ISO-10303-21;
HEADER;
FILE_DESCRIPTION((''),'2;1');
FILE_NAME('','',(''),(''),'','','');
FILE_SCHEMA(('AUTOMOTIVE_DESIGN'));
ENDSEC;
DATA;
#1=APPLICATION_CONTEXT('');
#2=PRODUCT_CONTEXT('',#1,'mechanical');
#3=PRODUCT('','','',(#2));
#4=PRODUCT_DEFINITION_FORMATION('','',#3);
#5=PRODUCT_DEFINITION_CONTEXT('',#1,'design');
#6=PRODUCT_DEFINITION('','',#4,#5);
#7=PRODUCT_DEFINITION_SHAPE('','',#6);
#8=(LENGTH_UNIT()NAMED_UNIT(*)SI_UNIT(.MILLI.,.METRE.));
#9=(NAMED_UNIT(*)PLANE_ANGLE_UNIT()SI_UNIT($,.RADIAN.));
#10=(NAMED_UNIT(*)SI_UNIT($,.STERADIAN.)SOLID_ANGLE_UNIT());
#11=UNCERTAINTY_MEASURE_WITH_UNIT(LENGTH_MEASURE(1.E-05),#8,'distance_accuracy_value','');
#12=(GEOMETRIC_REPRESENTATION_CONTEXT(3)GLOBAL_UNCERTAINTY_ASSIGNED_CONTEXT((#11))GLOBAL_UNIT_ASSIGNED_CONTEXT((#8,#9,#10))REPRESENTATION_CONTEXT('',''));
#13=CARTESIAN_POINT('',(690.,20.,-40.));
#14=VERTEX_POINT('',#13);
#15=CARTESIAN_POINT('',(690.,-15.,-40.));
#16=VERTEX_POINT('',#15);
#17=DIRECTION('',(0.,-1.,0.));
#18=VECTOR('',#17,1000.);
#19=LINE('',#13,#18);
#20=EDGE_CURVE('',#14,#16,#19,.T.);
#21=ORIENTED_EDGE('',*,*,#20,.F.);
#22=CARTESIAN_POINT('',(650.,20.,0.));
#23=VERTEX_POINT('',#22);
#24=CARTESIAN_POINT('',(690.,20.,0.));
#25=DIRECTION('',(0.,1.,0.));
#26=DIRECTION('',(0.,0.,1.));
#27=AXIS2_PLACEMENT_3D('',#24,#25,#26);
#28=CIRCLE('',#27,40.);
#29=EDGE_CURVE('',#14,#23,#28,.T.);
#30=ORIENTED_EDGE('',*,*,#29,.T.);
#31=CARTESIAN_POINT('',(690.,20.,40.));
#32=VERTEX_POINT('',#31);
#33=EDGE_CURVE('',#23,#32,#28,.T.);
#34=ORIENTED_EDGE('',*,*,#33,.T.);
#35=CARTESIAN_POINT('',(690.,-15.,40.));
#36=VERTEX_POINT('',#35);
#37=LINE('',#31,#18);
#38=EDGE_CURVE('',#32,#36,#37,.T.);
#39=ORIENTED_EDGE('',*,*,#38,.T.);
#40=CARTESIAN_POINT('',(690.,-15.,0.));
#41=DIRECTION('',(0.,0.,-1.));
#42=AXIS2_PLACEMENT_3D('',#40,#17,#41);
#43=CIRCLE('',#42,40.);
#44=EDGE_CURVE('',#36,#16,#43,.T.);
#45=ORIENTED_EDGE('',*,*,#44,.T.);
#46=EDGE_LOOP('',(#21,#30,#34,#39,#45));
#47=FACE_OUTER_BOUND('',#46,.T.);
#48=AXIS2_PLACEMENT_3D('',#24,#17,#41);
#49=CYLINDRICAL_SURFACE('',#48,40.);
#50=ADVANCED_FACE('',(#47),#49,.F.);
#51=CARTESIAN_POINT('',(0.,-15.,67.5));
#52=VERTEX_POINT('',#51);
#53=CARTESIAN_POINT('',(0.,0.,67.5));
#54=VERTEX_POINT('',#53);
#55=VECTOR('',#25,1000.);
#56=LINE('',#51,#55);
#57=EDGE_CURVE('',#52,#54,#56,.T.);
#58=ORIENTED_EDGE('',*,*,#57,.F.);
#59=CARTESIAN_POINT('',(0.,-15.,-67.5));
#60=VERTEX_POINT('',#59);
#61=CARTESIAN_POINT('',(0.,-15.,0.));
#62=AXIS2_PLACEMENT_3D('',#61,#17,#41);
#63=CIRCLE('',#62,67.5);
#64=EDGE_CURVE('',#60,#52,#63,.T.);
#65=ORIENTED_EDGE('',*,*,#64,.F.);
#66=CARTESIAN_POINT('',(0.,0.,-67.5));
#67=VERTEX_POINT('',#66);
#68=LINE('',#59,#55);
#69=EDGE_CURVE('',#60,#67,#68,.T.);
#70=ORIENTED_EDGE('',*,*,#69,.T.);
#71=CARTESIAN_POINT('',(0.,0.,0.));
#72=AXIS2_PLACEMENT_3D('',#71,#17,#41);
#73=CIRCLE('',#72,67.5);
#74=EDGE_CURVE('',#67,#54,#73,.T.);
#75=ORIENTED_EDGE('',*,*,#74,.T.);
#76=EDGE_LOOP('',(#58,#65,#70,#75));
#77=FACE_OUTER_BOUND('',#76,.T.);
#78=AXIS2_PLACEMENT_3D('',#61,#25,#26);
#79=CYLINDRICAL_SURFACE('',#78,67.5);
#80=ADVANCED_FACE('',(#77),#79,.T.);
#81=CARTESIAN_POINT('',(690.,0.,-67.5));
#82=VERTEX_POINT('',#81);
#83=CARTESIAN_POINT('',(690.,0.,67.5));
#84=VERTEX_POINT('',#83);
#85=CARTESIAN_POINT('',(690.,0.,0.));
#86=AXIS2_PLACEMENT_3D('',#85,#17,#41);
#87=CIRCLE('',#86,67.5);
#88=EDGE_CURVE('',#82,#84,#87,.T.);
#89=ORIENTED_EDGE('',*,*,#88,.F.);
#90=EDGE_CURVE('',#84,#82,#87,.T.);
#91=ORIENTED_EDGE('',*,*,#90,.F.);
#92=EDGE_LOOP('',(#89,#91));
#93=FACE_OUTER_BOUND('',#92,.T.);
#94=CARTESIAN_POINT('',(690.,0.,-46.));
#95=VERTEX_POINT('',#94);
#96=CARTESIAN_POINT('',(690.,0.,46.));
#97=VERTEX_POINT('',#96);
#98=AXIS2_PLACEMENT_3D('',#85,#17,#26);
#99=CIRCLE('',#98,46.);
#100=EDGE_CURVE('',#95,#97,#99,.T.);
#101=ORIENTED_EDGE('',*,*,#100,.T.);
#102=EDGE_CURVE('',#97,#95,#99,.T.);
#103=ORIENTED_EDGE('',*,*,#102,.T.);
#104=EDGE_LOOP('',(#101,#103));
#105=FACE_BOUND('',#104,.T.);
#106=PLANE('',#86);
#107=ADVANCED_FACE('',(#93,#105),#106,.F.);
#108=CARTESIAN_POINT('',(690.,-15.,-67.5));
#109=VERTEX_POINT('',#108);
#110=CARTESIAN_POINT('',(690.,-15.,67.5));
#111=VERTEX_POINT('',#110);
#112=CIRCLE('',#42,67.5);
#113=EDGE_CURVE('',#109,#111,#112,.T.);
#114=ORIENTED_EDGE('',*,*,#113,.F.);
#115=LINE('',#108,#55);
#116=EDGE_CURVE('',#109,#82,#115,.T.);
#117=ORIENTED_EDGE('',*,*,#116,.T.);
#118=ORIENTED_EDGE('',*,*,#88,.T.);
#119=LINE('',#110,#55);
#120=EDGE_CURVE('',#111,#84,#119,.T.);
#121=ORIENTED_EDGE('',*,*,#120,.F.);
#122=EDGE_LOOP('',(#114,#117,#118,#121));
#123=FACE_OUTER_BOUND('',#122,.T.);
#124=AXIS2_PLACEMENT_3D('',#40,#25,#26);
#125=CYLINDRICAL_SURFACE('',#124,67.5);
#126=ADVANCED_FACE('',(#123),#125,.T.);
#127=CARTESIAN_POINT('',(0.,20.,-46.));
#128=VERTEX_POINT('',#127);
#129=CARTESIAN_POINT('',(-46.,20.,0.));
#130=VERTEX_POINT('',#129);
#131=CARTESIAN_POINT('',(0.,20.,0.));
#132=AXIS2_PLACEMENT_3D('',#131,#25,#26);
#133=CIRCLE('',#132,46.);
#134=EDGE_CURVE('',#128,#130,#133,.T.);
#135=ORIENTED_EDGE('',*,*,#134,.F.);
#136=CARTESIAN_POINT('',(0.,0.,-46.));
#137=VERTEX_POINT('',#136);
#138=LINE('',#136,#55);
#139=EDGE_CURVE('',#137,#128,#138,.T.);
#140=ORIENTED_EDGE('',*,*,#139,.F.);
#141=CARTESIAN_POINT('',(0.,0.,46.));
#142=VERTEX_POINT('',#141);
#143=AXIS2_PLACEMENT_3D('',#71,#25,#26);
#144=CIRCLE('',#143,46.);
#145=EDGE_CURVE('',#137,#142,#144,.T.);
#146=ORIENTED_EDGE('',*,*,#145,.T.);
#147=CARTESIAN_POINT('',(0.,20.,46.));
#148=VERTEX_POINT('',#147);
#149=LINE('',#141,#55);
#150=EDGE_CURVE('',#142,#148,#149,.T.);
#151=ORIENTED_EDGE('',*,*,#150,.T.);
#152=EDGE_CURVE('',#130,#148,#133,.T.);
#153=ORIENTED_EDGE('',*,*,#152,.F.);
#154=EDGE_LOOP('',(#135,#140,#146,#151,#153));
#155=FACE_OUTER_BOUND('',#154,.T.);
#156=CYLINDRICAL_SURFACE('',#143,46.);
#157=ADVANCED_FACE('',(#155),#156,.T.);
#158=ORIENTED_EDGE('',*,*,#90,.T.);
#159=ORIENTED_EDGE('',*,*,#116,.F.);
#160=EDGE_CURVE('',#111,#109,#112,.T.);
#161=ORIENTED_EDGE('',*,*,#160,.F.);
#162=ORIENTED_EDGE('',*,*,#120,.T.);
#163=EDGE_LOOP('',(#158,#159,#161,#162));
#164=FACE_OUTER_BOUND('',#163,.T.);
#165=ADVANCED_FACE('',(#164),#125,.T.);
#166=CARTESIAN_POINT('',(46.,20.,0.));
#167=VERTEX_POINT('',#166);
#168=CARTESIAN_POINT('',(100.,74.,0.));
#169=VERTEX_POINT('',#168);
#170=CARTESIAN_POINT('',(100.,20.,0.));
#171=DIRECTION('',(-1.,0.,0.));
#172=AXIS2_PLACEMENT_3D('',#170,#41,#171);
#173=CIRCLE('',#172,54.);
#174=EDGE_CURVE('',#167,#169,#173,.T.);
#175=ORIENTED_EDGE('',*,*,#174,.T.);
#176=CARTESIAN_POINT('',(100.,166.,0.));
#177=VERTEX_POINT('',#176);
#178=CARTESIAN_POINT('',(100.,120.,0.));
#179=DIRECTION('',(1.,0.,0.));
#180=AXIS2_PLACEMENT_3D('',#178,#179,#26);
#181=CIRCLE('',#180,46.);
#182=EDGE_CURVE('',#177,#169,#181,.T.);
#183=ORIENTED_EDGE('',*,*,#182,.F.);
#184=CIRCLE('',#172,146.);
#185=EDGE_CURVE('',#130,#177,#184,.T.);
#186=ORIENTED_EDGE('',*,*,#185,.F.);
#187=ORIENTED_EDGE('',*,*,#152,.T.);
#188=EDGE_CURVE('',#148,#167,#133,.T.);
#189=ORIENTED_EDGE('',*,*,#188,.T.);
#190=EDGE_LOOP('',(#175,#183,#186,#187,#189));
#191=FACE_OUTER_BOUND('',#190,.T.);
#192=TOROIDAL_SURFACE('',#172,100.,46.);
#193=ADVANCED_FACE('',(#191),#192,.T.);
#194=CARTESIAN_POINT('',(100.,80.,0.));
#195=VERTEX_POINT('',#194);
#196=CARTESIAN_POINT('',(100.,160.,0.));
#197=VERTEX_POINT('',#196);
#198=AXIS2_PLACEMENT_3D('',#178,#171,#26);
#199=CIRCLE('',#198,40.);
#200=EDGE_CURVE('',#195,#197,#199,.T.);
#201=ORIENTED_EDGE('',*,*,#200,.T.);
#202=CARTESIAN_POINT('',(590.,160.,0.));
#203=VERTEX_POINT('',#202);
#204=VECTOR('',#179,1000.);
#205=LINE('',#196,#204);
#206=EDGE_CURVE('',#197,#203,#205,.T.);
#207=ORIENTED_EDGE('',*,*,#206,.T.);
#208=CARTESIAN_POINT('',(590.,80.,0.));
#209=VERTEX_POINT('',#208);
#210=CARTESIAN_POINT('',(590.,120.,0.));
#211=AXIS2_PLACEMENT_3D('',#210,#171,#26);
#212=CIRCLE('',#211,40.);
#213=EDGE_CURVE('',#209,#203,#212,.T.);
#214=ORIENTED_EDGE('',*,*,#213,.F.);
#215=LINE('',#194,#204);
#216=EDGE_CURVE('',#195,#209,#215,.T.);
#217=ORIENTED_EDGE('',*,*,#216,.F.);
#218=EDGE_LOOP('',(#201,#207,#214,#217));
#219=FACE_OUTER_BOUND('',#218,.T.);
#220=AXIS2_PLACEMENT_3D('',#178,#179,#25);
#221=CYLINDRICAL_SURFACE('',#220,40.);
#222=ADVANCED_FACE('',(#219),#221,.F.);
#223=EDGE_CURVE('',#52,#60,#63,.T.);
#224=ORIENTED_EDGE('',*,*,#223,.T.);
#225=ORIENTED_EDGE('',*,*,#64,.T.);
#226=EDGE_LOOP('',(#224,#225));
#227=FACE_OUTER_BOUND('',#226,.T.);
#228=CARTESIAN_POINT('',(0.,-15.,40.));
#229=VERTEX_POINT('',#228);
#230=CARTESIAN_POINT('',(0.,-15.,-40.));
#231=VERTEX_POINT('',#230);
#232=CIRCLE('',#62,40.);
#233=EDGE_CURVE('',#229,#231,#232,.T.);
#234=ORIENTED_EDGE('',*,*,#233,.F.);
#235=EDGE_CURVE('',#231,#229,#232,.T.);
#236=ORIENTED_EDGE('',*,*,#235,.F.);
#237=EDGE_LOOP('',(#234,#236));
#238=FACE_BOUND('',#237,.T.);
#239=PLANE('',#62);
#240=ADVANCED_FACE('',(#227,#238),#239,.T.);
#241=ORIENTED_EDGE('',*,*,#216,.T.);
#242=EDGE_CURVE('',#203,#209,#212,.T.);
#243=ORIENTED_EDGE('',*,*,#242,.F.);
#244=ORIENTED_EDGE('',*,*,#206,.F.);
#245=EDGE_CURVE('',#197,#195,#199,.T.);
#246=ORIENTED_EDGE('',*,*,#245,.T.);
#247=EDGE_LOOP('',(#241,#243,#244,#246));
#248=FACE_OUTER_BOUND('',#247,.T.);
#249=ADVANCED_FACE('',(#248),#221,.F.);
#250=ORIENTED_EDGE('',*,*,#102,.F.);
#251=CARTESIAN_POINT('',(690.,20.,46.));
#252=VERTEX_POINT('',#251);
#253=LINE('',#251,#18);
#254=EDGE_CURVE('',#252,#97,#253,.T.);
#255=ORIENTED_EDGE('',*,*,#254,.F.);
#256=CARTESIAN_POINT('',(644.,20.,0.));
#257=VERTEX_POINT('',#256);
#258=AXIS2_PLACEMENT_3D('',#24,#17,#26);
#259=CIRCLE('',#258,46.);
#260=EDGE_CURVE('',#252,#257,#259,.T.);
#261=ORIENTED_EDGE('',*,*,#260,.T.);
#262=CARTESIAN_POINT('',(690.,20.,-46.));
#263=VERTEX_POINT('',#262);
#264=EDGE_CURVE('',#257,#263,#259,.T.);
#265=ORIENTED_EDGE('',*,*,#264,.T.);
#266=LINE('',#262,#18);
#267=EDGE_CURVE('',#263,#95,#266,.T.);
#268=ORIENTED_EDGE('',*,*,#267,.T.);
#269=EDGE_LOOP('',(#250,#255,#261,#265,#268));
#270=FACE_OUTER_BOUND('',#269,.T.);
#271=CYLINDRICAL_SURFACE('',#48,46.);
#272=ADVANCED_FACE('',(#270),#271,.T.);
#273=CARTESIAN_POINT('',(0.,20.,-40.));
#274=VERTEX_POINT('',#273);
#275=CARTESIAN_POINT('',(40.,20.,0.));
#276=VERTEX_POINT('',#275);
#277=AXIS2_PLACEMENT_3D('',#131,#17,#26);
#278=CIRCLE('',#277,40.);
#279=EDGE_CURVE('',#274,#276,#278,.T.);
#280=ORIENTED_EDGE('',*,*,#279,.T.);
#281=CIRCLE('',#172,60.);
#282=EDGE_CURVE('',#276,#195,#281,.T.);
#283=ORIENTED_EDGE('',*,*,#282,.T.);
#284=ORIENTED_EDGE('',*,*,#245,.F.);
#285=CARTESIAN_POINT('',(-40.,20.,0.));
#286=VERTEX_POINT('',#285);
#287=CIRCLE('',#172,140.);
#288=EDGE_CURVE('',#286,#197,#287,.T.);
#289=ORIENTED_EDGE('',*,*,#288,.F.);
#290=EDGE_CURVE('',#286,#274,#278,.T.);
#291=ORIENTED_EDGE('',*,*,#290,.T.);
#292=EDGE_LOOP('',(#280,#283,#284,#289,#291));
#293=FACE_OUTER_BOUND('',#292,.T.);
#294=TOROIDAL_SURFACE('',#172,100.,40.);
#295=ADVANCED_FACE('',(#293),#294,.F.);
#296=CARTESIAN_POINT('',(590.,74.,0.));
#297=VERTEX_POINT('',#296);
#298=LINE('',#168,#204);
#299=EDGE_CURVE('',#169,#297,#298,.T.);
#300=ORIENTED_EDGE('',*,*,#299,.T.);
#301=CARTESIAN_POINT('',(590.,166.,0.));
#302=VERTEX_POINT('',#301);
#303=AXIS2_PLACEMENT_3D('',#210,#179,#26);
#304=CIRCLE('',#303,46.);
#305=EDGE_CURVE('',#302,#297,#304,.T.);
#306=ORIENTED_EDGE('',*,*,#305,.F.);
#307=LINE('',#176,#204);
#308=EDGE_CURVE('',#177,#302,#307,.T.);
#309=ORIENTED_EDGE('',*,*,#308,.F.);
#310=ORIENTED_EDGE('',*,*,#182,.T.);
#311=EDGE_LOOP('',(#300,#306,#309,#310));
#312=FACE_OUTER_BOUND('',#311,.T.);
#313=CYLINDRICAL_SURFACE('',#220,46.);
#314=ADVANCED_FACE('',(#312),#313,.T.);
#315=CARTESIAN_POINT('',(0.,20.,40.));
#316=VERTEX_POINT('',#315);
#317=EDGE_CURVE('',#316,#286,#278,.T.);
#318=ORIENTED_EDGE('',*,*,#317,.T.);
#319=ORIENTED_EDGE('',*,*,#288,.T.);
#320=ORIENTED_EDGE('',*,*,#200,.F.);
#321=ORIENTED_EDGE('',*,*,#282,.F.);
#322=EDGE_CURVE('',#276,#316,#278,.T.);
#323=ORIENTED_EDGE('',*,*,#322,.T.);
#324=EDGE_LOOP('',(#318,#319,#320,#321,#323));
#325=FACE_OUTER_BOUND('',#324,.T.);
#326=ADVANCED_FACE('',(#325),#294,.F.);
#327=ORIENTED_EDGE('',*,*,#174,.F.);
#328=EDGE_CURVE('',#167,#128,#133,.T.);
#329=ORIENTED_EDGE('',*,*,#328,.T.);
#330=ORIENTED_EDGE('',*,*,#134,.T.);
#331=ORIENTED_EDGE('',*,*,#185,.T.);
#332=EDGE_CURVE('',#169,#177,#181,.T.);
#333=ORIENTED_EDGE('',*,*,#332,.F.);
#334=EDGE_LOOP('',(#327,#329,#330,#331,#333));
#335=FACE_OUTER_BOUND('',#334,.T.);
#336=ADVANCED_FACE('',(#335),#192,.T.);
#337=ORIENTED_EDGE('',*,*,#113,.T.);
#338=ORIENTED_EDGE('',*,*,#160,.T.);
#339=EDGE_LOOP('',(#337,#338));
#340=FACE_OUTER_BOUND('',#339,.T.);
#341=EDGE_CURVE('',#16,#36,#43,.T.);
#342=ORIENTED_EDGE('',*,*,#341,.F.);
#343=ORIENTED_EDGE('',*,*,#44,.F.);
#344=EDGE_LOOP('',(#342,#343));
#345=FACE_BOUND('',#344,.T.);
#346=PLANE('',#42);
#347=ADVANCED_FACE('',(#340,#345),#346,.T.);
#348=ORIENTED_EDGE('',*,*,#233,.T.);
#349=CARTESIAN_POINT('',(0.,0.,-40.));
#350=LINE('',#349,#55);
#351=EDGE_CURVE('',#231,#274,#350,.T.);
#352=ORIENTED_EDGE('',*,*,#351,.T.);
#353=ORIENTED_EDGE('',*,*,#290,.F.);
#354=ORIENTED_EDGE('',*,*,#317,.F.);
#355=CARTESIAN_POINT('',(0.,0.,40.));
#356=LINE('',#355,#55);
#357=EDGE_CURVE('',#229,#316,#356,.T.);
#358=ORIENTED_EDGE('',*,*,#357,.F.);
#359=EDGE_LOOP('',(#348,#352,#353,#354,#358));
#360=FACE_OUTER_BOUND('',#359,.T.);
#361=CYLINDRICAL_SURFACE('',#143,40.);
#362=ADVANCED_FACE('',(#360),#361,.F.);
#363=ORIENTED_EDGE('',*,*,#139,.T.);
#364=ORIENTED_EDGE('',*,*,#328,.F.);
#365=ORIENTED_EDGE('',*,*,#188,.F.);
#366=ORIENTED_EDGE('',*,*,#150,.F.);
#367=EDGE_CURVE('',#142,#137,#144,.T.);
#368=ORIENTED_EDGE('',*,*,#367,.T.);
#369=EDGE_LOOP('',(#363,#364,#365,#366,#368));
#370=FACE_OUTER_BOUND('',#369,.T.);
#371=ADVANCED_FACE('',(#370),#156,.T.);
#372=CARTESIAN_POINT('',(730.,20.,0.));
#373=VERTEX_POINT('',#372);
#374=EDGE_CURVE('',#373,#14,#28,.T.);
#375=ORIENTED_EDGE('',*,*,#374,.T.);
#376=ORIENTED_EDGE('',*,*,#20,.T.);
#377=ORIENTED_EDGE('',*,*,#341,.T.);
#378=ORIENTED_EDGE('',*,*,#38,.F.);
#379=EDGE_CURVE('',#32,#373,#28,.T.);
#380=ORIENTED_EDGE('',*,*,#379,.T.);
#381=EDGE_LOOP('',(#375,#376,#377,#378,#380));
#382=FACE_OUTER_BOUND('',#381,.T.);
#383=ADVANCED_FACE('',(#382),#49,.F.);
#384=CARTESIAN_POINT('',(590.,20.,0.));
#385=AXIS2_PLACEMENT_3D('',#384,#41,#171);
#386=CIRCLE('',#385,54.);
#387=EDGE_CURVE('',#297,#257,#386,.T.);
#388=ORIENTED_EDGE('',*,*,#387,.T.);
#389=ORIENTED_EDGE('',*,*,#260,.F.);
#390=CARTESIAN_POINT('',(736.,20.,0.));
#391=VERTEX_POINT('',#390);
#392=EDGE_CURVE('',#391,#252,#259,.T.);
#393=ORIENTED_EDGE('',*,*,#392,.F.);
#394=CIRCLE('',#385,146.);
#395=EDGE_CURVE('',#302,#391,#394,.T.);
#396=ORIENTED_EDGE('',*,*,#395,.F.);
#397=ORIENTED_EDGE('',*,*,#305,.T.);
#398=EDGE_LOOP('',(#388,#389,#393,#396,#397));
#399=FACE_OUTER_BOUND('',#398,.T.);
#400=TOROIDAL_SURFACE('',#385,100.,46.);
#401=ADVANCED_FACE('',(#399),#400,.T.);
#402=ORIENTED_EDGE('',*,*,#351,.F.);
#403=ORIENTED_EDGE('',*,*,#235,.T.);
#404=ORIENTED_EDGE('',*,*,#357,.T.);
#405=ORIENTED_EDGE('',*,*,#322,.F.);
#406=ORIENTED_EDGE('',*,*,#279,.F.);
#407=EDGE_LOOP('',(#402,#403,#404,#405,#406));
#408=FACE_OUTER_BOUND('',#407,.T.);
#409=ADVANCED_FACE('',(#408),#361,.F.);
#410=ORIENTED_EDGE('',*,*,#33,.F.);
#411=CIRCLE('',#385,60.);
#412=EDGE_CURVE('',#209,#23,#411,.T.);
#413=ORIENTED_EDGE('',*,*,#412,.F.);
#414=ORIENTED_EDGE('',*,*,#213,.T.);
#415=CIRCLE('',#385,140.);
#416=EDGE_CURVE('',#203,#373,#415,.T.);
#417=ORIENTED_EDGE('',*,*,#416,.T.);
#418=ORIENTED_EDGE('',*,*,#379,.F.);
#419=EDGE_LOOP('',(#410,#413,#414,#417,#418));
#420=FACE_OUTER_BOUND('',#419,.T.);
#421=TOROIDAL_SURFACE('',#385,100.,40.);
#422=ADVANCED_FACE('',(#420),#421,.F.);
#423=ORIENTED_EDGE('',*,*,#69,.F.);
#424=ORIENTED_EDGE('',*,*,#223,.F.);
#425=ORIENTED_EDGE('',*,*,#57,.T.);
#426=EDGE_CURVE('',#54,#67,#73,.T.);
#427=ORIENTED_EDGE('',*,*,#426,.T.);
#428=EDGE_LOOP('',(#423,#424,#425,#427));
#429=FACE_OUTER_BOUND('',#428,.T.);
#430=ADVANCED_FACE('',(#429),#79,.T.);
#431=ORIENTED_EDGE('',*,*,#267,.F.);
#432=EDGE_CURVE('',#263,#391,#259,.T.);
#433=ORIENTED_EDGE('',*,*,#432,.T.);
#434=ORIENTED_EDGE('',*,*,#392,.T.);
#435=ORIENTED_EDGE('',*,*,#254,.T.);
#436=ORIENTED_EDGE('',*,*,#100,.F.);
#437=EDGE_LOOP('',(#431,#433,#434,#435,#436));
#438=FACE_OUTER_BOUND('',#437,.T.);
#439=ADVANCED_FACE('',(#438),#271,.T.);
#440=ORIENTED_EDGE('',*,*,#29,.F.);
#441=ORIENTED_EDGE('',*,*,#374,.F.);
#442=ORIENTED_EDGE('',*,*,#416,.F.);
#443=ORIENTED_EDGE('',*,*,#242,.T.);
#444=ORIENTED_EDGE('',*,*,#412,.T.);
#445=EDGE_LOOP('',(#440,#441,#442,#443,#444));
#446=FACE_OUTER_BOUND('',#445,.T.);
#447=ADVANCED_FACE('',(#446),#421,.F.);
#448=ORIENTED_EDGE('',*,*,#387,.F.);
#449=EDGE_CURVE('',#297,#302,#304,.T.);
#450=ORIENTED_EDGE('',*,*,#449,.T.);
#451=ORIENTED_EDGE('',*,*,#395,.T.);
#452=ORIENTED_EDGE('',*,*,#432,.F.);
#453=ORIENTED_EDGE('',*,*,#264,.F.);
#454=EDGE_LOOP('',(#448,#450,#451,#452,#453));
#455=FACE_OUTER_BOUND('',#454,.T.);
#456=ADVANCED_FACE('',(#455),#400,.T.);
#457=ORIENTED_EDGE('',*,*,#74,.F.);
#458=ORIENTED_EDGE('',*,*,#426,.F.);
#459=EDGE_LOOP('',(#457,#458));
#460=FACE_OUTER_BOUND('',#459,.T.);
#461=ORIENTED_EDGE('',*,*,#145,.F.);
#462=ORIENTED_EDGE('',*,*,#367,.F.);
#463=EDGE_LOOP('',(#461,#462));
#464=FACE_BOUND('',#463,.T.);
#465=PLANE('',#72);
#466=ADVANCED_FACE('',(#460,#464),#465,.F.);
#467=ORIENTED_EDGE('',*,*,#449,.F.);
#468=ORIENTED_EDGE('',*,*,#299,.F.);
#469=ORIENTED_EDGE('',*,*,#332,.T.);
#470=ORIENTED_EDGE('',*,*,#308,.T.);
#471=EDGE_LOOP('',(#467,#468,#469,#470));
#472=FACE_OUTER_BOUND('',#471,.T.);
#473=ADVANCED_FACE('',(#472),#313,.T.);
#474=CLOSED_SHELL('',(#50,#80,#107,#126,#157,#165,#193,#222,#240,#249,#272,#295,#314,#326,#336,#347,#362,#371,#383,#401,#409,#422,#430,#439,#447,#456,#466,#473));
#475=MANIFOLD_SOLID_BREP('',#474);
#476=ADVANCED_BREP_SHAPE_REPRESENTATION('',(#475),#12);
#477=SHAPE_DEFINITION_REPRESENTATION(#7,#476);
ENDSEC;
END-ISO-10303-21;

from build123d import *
from build123d.topology import SkipClean

# Parameters (mm, degrees)
SKETCH2_R           = 46
SKETCH2_R_2         = 40
SKETCH4_R           = 67.5
SKETCH4_R_2         = 40
BOSS_EXTRUDE1_DEPTH = 15


with BuildPart() as part:
    # Sweep1: sweep along a path in Sketch3
    with BuildLine(Plane.XY) as sweep1_path:
        Line((0, 0), (0, 20))
        ThreePointArc((0, 20), (29.289321881, 90.710678119), (100, 120))
        Line((100, 120), (590, 120))
        ThreePointArc((590, 120), (660.710678119, 90.710678119), (690, 20))
        Line((690, 20), (690, 0))
    # Sketch2 → Sweep1 (sweep)
    with BuildSketch(Plane(origin=(0, 0, 0), x_dir=(1, 0, 0), z_dir=(0, 1, 0))):
        Circle(SKETCH2_R)
        Circle(SKETCH2_R_2, mode=Mode.SUBTRACT)
    sweep(path=sweep1_path.line)

    # Sketch4 → Boss-Extrude1 (add)
    # profile 1 of 2: a face of its own
    with SkipClean():  # the faces are left unmerged after this step: merging them gives an invalid solid
        with BuildSketch(Plane(origin=(0, 0, 0), x_dir=(-1, 0, 0), z_dir=(0, -1, 0))):
            with Locations(Location((0, 0, 0), (0, 0, 90))):
                Circle(SKETCH4_R)
            Circle(SKETCH4_R_2, mode=Mode.SUBTRACT)
        # profile 2 of 2: a face of its own
        with BuildSketch(Plane(origin=(0, 0, 0), x_dir=(-1, 0, 0), z_dir=(0, -1, 0))):
            with Locations(Location((-690, 0, 0), (0, 0, 90))):
                Circle(SKETCH4_R)
            with Locations(Location((-690, 0, 0), (0, 0, 90))):
                Circle(SKETCH4_R_2, mode=Mode.SUBTRACT)
        extrude(amount=BOSS_EXTRUDE1_DEPTH)


solid = part.part
